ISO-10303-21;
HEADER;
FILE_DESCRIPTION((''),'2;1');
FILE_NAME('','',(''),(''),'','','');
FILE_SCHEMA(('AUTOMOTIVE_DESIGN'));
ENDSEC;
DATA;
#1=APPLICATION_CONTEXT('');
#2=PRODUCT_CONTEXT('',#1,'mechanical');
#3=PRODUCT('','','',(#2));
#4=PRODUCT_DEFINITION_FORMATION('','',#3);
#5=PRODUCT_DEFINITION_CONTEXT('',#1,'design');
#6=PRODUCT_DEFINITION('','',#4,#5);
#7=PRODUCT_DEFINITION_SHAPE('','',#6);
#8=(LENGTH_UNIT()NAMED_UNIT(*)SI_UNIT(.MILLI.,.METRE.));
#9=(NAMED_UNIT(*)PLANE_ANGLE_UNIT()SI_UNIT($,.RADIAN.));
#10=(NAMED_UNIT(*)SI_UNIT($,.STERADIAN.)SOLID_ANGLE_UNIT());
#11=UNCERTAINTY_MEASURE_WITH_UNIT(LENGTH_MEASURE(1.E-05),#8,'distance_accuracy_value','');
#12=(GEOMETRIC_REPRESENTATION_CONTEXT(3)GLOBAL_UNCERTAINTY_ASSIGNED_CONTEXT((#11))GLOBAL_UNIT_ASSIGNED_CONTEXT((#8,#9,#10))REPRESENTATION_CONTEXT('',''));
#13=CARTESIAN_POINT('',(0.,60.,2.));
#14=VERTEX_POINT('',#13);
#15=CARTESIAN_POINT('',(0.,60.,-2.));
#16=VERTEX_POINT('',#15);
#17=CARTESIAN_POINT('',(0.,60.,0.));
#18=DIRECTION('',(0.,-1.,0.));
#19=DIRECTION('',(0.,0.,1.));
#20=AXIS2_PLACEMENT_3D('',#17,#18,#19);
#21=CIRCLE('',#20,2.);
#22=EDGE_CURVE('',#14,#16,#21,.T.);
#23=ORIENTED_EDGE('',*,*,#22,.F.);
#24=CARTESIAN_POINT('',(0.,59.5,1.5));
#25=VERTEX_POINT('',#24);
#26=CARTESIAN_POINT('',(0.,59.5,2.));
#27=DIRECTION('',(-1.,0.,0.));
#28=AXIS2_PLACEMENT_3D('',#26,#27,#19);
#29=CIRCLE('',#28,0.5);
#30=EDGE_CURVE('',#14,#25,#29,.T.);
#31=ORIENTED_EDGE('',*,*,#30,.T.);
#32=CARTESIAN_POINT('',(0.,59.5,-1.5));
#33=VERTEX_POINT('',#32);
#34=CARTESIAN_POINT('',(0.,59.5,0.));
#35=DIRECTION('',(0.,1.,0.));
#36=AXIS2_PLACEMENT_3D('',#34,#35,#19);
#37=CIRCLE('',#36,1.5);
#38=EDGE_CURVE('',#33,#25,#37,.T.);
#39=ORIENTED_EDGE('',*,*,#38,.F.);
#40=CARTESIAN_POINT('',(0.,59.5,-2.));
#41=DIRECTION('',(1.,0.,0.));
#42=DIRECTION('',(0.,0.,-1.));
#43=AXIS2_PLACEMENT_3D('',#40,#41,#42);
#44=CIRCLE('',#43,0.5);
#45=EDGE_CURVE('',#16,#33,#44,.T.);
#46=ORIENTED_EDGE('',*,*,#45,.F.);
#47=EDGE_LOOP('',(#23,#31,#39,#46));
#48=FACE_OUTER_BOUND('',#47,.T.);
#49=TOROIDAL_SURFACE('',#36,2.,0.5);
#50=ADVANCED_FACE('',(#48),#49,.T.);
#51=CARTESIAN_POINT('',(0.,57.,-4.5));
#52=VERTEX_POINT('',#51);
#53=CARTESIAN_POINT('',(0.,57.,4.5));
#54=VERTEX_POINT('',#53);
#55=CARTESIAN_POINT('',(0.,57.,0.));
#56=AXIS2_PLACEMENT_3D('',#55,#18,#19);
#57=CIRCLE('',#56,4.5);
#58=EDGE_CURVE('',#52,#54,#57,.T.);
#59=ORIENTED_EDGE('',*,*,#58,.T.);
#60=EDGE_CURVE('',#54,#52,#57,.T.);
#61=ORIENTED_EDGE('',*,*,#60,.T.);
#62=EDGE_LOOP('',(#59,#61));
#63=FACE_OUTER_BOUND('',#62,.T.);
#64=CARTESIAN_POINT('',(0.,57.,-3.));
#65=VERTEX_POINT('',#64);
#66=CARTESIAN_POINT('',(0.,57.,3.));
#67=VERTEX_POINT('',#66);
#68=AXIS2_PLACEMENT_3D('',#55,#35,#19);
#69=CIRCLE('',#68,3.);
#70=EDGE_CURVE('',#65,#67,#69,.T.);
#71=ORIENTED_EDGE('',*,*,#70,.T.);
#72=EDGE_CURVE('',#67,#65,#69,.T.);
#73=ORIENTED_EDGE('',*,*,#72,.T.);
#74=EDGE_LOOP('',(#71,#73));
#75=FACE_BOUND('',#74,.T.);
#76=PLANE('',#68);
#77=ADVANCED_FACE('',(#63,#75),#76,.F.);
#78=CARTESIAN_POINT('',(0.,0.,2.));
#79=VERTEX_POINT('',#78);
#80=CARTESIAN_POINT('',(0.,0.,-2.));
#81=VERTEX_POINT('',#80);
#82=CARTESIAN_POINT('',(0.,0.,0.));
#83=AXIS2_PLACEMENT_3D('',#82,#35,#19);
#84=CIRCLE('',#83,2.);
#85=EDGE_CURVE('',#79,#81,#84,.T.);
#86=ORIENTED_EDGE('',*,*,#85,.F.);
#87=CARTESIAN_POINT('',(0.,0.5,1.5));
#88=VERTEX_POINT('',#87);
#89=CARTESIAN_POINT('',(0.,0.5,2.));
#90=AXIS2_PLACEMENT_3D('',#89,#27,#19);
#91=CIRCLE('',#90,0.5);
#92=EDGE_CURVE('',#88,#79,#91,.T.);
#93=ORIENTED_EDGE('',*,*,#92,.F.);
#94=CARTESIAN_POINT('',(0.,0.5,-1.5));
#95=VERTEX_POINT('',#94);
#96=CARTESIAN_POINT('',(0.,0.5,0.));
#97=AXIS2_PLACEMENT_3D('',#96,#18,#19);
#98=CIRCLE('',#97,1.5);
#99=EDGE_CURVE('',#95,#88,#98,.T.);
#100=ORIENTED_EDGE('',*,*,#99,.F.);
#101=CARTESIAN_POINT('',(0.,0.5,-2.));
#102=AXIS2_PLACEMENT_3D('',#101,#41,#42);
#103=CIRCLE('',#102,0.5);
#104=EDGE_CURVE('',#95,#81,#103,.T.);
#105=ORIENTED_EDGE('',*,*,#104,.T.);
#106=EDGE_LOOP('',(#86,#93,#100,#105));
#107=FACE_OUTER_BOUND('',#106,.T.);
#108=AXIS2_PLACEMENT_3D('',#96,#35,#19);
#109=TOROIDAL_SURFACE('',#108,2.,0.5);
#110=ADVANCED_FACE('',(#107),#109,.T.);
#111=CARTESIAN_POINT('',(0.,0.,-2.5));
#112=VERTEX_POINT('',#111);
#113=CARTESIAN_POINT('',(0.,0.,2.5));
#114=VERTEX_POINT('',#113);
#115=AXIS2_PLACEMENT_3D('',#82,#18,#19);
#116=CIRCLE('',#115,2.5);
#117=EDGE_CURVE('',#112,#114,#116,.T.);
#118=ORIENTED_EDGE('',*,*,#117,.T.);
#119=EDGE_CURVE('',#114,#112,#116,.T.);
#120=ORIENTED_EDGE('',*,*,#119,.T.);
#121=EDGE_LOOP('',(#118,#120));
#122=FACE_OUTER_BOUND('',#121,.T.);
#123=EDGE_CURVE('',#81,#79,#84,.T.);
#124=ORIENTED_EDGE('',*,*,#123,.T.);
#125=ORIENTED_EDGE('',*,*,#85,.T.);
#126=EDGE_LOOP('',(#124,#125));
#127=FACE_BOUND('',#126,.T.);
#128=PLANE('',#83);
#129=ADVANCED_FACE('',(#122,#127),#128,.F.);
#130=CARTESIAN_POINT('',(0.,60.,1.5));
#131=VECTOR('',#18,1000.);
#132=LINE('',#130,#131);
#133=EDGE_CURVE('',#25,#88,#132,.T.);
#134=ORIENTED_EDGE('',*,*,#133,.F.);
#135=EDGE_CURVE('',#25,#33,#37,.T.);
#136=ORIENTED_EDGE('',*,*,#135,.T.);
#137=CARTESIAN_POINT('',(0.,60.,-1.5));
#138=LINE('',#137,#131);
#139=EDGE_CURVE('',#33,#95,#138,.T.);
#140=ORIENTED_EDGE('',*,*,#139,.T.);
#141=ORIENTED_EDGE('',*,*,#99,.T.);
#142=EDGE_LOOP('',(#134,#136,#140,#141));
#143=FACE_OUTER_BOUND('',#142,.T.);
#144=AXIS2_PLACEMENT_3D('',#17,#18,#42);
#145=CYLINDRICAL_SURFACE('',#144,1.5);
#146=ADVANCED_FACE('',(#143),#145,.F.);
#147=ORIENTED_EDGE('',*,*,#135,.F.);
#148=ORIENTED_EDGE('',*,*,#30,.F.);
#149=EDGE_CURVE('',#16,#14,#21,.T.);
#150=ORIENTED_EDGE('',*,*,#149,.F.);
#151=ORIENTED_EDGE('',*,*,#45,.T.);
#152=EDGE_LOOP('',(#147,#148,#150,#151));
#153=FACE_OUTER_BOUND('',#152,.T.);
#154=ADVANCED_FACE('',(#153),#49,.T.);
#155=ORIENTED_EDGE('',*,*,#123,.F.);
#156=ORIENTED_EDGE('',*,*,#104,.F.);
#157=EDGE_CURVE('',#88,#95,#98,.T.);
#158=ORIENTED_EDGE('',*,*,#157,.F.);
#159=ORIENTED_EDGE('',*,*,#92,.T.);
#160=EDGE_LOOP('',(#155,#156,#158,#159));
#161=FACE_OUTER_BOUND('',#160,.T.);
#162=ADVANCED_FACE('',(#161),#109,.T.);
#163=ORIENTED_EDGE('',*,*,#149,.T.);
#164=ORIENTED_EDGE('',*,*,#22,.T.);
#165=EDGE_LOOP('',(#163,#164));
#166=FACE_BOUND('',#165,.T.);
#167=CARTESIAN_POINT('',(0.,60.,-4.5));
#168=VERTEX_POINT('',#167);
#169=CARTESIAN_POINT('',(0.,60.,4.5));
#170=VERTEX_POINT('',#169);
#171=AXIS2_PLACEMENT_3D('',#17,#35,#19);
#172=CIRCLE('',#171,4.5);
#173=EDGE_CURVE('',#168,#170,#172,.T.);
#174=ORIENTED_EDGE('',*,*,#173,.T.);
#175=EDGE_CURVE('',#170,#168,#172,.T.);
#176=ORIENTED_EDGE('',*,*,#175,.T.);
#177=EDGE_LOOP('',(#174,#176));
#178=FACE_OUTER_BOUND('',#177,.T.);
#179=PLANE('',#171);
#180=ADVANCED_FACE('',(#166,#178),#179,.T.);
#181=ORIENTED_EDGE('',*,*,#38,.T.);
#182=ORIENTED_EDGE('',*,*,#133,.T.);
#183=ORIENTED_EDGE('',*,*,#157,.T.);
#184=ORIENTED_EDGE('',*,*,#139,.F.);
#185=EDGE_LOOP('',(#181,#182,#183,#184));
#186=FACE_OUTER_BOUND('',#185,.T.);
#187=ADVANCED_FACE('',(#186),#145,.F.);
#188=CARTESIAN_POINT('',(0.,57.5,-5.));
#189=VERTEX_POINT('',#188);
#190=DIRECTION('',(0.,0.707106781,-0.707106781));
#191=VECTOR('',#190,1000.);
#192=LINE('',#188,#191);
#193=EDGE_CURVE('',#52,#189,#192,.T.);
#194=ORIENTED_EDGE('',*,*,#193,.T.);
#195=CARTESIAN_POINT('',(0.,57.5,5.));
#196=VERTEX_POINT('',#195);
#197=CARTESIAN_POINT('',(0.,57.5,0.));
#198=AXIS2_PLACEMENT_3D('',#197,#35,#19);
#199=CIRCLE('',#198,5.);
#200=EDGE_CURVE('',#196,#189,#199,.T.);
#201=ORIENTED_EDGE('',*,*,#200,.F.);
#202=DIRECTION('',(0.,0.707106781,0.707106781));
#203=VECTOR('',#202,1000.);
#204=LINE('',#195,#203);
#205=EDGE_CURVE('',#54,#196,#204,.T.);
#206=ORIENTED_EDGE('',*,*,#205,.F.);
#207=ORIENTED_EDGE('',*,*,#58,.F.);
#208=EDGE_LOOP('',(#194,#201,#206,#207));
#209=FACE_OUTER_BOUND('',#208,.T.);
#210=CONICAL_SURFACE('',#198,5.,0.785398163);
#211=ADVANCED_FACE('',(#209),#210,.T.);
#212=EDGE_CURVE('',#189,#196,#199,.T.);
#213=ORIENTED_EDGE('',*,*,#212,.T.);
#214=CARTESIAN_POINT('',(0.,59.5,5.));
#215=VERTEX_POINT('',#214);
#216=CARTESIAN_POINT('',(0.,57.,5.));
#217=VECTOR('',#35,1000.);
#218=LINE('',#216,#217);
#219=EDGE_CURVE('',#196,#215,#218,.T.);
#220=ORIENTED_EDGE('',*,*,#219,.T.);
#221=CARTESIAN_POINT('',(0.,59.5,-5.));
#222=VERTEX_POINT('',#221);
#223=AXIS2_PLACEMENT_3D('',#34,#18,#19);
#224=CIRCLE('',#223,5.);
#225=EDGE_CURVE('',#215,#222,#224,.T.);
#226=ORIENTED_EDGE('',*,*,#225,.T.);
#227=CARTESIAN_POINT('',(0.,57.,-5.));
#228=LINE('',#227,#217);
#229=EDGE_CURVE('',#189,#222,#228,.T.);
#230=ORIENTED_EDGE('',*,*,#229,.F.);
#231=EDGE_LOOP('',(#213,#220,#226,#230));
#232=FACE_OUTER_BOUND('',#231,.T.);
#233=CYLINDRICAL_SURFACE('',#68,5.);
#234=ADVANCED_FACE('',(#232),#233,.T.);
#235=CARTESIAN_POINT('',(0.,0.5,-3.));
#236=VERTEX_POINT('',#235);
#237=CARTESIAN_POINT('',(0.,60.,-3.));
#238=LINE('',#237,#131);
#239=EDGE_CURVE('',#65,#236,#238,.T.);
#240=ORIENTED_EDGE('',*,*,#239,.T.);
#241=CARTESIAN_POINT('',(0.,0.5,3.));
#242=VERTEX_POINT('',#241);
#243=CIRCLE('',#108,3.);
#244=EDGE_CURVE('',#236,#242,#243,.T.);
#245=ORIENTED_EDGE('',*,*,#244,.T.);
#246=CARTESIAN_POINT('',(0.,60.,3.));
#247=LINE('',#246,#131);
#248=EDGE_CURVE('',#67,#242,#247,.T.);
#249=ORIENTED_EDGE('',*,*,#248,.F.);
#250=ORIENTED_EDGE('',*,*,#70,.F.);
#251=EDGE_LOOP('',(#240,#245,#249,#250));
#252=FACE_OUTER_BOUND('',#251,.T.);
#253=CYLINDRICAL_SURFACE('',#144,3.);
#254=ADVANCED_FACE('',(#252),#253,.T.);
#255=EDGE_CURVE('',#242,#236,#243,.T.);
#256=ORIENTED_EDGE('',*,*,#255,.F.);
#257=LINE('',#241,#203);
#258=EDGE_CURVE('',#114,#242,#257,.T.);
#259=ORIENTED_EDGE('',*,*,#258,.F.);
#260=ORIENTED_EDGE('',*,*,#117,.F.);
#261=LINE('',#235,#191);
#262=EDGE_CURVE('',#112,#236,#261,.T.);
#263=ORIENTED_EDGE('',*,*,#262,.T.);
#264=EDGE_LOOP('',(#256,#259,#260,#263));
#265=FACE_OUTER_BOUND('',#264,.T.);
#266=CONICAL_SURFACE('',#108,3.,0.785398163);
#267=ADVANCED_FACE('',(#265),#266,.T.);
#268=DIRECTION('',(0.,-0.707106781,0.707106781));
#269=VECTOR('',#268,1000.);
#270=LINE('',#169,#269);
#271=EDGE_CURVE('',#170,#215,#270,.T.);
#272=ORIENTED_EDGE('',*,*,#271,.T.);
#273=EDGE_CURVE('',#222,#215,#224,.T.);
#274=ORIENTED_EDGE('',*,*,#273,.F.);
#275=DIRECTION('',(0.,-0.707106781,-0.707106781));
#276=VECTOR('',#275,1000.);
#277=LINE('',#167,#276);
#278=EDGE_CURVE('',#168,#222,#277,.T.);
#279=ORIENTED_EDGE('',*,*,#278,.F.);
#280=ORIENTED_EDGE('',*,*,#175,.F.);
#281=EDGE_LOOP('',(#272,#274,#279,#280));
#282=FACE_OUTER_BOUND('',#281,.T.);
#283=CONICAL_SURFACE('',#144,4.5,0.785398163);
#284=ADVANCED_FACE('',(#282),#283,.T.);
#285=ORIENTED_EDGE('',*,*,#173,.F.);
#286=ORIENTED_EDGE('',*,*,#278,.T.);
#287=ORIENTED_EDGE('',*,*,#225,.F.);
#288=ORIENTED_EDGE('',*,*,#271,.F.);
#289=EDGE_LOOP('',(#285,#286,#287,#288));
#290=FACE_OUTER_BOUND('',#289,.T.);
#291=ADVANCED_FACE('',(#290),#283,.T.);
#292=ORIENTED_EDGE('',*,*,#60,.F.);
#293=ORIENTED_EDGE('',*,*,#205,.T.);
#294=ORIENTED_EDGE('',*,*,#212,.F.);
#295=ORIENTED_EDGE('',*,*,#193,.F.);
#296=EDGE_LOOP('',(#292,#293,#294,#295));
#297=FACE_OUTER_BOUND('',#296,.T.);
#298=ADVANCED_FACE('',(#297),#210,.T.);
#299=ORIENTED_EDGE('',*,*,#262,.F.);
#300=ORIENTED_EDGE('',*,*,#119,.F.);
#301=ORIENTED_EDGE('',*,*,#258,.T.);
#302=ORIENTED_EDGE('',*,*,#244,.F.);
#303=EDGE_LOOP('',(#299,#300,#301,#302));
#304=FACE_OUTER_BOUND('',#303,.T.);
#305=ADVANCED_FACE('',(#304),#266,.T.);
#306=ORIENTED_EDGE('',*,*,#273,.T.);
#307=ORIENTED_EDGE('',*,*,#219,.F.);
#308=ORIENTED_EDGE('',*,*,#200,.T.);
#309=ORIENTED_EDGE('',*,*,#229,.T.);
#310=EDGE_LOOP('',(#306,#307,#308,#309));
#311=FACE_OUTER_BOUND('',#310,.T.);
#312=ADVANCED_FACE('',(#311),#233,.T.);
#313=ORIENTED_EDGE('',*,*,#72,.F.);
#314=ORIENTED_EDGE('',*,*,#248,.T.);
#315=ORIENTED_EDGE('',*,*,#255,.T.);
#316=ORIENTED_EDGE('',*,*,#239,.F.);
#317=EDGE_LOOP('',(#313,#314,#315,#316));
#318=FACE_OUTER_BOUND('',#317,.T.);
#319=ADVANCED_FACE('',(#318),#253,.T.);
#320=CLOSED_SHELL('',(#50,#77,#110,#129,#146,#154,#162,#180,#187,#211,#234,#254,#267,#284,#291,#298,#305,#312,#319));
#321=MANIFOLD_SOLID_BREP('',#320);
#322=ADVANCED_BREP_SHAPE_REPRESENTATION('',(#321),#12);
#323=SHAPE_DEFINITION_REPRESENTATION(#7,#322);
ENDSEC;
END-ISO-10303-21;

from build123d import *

# Parameters (mm, degrees)
SKETCH_1_R      = 3
SKETCH_1_R_2    = 1.5
EXTRUDE_1_DEPTH = 60
EXTRUDE_START   = -3
SKETCH_2_R      = 5
SKETCH_2_R_2    = 1.5
EXTRUDE_2_DEPTH = 3
FILLET_1_R      = 0.5
CHAMFER_1_SIZE  = 0.5


with BuildPart() as part:
    # 草图1 → 凸台-拉伸1 (new body)
    with BuildSketch(Plane(origin=(0, 0, 0), x_dir=(1, 0, 0), z_dir=(0, 1, 0))):
        with Locations(Location((0, 0, 0), (0, 0, 270))):
            Circle(SKETCH_1_R)
        with Locations(Location((0, 0, 0), (0, 0, 270))):
            Circle(SKETCH_1_R_2, mode=Mode.SUBTRACT)
    extrude(amount=EXTRUDE_1_DEPTH)

    # 草图2 → 凸台-拉伸2 (add)
    with BuildSketch(Plane(origin=(0, 60, 0), x_dir=(1, 0, 0), z_dir=(0, 1, 0)).offset(EXTRUDE_START)):
        with Locations(Location((0, 0, 0), (0, 0, 270))):
            Circle(SKETCH_2_R)
        with Locations(Location((0, 0, 0), (0, 0, 270))):
            Circle(SKETCH_2_R_2, mode=Mode.SUBTRACT)
    extrude(amount=EXTRUDE_2_DEPTH)

    # 圆角1
    fillet_1_edges = [part.edges().sort_by_distance(p)[0] for p in [
        (0, 0, -1.5),
        (0, 60, -1.5),
    ]]
    fillet(fillet_1_edges, radius=FILLET_1_R)

    # 倒角1
    chamfer_1_edges = [part.edges().sort_by_distance(p)[0] for p in [
        (0, 60, -5),
        (0, 57, -5),
        (0, 0, -3),
    ]]
    chamfer(chamfer_1_edges, length=CHAMFER_1_SIZE)


solid = part.part
